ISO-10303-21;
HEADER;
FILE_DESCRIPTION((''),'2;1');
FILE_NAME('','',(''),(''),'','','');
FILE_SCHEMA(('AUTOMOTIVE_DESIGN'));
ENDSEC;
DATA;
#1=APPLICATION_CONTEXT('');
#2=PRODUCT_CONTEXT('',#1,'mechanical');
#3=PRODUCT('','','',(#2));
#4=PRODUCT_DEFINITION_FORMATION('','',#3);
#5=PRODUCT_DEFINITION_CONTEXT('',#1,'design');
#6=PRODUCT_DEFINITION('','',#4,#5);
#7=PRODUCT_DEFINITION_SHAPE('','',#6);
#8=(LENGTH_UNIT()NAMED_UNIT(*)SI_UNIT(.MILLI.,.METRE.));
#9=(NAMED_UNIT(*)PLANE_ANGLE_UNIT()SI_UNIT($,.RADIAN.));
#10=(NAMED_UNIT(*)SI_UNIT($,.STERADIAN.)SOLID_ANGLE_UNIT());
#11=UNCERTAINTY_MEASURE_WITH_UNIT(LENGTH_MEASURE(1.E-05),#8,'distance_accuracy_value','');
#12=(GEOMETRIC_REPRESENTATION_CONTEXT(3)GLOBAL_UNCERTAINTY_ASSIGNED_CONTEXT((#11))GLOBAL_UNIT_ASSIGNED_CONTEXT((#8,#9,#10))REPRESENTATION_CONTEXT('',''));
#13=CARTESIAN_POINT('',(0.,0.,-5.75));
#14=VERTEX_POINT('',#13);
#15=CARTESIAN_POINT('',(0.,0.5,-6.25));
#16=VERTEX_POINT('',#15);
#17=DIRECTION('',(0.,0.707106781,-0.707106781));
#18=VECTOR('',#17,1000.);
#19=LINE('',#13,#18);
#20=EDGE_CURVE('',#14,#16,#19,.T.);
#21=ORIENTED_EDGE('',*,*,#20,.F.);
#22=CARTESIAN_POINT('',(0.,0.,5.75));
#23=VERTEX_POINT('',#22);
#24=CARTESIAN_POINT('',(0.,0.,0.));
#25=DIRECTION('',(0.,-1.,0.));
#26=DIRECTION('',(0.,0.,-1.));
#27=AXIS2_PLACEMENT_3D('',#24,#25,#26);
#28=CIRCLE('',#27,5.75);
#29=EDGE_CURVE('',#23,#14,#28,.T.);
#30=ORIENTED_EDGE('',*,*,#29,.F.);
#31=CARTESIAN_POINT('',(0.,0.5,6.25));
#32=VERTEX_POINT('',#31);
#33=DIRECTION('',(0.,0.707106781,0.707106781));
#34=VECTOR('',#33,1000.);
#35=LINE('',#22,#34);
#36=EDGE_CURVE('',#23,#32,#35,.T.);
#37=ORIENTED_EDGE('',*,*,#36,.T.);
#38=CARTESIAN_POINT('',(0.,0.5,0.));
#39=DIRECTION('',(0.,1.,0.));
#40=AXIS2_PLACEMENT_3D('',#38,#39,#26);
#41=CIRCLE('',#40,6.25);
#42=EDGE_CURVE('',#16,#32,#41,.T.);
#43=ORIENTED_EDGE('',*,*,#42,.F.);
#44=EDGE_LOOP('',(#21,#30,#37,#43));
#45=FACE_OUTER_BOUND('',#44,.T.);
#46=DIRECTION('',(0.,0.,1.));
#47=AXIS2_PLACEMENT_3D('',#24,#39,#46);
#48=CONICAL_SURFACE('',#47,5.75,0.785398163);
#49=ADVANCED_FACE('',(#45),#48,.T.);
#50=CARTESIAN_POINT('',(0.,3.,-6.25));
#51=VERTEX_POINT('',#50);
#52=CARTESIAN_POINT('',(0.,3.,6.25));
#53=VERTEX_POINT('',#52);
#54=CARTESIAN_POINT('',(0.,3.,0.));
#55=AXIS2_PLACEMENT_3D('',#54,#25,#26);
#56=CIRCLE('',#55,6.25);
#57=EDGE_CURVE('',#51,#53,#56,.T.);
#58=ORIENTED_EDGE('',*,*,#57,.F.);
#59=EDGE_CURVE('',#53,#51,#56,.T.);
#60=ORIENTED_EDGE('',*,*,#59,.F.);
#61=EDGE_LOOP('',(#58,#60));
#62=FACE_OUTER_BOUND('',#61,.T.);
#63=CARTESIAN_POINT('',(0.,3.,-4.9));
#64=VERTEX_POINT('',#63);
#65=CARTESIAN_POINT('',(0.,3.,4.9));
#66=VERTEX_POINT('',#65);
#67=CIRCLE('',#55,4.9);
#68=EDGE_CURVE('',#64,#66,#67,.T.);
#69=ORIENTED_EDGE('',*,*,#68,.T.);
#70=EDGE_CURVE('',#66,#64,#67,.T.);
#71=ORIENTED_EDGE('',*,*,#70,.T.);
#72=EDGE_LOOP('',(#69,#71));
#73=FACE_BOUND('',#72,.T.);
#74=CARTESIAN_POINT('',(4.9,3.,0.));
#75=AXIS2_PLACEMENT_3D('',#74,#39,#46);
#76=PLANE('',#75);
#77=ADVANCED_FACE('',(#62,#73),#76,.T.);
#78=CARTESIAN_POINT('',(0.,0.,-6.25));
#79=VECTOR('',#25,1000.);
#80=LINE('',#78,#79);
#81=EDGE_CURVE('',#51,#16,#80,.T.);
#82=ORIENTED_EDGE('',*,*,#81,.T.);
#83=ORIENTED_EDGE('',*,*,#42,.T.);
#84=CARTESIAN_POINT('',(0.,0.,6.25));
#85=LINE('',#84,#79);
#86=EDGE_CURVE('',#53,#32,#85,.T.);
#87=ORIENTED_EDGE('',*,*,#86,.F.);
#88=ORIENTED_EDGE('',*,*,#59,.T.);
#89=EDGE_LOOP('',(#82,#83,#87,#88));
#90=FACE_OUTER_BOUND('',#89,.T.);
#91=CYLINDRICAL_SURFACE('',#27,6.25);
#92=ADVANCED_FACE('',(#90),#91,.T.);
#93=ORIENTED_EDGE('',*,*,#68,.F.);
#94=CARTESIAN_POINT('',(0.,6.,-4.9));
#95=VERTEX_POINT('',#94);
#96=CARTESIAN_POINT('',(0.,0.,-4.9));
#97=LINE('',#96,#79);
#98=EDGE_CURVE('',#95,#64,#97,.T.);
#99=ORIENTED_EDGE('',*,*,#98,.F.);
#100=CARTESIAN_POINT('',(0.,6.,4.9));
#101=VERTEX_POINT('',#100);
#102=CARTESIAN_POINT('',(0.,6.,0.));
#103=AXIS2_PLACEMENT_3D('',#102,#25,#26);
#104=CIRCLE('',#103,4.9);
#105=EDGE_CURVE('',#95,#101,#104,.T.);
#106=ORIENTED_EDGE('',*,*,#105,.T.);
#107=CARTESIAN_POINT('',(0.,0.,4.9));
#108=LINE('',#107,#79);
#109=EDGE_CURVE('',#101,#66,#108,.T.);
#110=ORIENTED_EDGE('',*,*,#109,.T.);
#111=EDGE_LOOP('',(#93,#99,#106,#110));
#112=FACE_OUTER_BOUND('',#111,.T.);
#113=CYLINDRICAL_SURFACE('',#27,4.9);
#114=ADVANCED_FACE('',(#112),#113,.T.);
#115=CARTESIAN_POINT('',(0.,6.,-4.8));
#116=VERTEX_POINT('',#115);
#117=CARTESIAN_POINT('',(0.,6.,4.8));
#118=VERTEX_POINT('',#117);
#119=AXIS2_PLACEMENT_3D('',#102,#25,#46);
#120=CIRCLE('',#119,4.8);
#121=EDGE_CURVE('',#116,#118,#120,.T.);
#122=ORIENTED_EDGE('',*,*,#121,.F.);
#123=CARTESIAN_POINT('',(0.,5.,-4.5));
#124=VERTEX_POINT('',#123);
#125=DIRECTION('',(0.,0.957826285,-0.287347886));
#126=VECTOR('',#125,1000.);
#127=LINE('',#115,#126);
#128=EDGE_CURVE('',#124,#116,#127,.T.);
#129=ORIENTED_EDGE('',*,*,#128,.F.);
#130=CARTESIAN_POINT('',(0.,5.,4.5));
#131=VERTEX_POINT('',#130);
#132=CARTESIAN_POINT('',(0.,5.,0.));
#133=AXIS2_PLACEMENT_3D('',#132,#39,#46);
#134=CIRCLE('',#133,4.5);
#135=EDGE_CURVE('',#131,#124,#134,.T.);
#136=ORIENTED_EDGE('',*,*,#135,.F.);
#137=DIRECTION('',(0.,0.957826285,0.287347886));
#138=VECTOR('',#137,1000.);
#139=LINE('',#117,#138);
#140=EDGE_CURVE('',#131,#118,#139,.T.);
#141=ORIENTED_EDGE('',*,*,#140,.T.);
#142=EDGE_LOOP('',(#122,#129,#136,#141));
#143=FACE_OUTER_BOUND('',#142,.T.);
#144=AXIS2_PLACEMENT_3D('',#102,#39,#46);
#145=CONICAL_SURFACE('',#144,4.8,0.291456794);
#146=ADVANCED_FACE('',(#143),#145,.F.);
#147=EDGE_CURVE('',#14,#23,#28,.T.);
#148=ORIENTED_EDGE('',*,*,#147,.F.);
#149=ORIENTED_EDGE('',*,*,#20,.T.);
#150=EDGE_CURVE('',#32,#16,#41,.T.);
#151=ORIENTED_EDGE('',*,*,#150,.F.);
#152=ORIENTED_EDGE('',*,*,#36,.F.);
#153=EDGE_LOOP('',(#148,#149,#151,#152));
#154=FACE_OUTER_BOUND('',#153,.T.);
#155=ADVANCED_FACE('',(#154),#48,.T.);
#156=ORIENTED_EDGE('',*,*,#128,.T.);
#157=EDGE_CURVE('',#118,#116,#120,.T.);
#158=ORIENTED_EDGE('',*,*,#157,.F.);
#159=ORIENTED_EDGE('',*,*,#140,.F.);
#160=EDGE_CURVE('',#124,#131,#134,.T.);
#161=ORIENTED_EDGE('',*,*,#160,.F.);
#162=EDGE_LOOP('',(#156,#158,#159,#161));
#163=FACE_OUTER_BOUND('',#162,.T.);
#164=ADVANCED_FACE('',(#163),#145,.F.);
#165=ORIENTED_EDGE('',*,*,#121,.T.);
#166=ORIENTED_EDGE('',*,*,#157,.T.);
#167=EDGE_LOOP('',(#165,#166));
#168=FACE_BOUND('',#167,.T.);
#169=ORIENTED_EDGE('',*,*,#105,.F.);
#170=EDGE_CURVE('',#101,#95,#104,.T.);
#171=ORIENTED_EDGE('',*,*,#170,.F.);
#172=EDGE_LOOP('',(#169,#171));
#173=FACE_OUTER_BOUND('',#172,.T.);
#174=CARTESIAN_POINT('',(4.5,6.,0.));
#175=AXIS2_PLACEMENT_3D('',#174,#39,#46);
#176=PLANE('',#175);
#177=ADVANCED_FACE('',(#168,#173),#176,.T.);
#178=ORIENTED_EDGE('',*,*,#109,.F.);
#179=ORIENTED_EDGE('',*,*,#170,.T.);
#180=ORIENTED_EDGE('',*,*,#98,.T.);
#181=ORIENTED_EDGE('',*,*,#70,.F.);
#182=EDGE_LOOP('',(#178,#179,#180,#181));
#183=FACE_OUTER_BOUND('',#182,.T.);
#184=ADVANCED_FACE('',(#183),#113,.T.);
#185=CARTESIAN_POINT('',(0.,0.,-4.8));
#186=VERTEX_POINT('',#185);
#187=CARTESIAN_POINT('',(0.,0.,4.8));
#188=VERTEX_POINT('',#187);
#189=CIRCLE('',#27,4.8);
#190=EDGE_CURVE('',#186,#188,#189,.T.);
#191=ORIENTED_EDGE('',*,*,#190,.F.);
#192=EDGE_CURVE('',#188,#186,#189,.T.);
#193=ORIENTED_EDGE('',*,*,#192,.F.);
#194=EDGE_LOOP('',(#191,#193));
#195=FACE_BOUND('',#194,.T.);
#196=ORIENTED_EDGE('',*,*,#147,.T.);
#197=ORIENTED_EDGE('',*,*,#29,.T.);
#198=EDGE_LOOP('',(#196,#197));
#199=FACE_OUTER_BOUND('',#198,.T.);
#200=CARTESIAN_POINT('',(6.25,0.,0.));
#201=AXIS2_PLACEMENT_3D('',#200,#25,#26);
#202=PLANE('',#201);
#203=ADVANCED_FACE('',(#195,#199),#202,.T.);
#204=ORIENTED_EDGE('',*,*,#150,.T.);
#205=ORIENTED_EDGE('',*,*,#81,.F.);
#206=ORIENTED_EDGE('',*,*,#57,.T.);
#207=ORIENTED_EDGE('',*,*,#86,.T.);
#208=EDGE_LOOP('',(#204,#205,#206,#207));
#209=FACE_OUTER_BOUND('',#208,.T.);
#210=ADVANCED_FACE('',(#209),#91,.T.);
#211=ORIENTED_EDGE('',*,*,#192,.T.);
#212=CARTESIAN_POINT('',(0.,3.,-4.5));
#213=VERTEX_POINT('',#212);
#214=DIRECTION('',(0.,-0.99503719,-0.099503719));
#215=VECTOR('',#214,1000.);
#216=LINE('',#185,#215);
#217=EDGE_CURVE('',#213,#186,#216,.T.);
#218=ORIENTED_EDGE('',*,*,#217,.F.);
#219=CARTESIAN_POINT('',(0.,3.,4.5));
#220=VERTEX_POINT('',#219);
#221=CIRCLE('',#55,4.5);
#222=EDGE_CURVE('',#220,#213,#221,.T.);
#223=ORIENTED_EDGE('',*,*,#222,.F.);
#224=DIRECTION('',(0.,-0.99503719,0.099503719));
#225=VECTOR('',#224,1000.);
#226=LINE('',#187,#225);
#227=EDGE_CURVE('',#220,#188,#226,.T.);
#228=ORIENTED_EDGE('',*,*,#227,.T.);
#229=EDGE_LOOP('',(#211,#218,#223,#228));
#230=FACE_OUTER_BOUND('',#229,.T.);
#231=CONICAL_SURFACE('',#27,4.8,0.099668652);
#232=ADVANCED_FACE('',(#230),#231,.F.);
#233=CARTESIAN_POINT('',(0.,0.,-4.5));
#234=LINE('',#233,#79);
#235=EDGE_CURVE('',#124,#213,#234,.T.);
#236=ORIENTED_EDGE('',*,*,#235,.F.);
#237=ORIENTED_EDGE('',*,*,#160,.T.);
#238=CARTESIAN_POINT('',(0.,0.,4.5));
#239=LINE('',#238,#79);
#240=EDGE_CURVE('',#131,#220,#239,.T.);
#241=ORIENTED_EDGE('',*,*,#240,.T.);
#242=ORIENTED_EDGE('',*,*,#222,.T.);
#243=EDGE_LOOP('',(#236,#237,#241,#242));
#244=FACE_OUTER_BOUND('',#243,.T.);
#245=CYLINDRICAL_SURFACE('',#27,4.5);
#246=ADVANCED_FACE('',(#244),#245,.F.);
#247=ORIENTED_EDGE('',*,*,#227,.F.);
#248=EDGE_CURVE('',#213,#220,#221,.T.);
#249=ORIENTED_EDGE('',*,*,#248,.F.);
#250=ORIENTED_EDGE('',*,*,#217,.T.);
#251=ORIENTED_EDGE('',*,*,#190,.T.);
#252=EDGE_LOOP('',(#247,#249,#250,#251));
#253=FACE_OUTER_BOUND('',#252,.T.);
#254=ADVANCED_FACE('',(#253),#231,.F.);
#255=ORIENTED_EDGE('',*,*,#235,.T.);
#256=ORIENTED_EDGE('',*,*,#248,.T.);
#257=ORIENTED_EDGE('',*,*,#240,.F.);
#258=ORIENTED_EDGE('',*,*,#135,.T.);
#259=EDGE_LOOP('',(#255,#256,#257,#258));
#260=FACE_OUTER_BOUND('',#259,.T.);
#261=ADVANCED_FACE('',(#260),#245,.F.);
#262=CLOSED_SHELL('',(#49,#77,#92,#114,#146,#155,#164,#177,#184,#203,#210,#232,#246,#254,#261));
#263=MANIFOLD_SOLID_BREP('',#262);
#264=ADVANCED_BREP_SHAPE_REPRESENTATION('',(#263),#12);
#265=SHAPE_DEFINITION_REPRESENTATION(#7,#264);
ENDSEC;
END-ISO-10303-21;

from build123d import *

# Parameters (mm, degrees)
CHAMFER1_SIZE  = 0.5
CHAMFER2_SIZE  = 1
CHAMFER2_SIZE2 = 0.3


with BuildPart() as part:
    # Sketch2 → Revolve1 (revolve)
    with BuildSketch(Plane.XY, mode=Mode.PRIVATE) as revolve1_sk:
        Polygon((4.5, 0), (4.5, 6), (4.9, 6), (4.9, 3), (6.25, 3), (6.25, 0), align=None)
    revolve(revolve1_sk.sketch.rotate(Axis((0, 0, 0), (0, 1, 0)), 90), axis=Axis((0, 0, 0), (0, 1, 0)))

    # Sketch3 → Cut-Revolve1 (revolve, cut)
    with BuildSketch(Plane.XY, mode=Mode.PRIVATE) as cut_revolve1_sk:
        Polygon((4.5, 3), (4.5, 0), (4.8, 0), align=None)
    revolve(cut_revolve1_sk.sketch.rotate(Axis((0, 0, 0), (0, 1, 0)), 90), axis=Axis((0, 0, 0), (0, 1, 0)), mode=Mode.SUBTRACT)

    # Chamfer1
    chamfer1_edges = [part.edges().sort_by_distance(p)[0] for p in [
        (0, 0, 6.25),
    ]]
    chamfer(chamfer1_edges, length=CHAMFER1_SIZE)

    # Chamfer2
    chamfer2_edges = [part.edges().sort_by_distance(p)[0] for p in [
        (0, 6, 4.5),
    ]]
    chamfer2_side = [part.faces().sort_by_distance(p)[0] for p in [
        (0, 4.5, 4.5),
    ]]
    chamfer(chamfer2_edges, length=CHAMFER2_SIZE, length2=CHAMFER2_SIZE2, reference=chamfer2_side[0])


solid = part.part
